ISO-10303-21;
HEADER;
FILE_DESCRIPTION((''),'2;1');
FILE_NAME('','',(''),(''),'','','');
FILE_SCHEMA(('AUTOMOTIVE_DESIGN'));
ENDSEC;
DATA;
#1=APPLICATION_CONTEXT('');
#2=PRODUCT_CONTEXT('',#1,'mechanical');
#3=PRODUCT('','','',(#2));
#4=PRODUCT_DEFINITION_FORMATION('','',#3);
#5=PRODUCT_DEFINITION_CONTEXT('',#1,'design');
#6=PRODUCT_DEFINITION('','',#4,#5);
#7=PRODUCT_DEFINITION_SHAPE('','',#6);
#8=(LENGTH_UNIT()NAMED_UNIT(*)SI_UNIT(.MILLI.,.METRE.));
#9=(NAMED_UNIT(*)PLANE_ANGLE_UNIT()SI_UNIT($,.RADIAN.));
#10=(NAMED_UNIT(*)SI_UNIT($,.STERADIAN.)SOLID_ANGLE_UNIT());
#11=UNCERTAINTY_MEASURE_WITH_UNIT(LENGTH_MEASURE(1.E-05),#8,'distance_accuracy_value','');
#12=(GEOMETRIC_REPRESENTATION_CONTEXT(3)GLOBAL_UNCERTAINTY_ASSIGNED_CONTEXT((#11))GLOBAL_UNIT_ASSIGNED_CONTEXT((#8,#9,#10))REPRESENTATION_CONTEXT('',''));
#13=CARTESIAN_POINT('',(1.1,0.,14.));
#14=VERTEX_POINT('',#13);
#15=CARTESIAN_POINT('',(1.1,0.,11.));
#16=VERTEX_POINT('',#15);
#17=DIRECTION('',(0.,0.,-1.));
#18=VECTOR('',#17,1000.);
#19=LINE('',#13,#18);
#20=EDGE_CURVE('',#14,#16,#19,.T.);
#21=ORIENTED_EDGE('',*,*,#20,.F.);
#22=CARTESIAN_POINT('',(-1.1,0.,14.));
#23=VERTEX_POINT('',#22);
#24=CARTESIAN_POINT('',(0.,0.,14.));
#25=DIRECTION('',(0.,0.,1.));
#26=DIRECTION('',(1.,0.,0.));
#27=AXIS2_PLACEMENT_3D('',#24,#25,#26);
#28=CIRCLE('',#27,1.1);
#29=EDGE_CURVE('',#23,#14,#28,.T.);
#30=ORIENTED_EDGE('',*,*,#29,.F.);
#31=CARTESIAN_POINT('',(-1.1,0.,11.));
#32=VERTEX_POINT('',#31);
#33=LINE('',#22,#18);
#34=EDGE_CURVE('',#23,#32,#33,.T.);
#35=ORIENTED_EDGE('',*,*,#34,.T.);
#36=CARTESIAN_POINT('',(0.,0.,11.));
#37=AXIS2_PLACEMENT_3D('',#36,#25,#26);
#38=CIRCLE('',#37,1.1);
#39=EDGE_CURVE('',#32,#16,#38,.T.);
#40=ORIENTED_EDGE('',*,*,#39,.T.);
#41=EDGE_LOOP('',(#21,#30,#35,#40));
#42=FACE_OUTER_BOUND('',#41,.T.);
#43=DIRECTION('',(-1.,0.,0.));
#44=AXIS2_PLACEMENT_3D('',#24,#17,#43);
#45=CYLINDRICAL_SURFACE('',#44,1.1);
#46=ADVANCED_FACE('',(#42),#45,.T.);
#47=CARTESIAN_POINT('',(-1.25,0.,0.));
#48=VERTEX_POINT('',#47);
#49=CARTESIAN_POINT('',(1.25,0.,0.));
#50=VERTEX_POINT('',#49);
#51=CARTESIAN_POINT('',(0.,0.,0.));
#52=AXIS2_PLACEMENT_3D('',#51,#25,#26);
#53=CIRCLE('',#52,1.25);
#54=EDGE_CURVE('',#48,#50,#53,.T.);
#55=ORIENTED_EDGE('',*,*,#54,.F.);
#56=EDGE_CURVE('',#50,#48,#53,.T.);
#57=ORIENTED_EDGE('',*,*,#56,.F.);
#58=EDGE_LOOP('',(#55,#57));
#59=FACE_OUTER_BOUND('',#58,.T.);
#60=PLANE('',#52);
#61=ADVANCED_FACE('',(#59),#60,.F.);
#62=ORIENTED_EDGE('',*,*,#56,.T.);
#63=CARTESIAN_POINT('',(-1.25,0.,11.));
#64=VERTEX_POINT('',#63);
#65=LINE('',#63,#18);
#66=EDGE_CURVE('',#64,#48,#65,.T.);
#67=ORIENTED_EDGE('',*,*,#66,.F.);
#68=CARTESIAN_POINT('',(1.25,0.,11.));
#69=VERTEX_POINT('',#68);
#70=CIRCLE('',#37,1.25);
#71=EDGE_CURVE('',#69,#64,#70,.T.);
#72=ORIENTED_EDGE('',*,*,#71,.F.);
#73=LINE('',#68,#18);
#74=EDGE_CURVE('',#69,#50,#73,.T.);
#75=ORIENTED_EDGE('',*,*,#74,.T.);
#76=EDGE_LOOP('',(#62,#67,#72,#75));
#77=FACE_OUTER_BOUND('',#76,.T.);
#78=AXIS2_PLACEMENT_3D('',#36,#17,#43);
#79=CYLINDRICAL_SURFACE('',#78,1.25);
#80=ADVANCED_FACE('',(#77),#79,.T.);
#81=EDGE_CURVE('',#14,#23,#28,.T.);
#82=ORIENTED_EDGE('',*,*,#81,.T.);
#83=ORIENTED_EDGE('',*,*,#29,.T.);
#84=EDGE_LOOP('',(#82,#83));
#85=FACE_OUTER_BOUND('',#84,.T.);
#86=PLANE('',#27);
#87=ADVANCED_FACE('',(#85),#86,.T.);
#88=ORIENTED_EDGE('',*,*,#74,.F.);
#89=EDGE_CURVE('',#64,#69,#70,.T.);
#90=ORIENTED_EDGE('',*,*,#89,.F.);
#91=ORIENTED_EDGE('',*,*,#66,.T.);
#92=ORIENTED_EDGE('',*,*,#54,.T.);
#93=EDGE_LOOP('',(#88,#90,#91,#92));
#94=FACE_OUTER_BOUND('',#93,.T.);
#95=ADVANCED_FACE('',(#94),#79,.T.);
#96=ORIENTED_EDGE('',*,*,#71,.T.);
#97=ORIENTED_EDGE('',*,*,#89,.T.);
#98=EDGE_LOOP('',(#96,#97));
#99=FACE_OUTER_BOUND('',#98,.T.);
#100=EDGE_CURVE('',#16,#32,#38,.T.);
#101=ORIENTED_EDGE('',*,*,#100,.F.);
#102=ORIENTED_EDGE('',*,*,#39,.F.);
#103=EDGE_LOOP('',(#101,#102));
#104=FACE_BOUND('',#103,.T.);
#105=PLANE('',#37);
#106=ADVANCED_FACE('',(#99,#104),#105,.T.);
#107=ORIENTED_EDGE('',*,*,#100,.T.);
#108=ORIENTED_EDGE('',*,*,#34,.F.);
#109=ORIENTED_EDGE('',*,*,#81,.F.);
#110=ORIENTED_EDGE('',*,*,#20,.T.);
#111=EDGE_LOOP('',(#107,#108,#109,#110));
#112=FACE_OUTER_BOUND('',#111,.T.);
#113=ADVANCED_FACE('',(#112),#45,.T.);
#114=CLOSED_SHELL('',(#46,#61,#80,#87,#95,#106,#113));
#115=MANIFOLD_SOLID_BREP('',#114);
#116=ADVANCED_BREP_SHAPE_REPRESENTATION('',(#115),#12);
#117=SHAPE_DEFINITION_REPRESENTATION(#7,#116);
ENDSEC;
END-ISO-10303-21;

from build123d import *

# Parameters (mm, degrees)
SKETCH_1_R      = 1.25
EXTRUDE_1_DEPTH = 11
SKETCH_2_R      = 1.1
EXTRUDE_2_DEPTH = 3


with BuildPart() as part:
    # 草图1 → 凸台-拉伸1 (new body)
    with BuildSketch(Plane.XY):
        Circle(SKETCH_1_R)
    extrude(amount=EXTRUDE_1_DEPTH)

    # 草图2 → 凸台-拉伸2 (add)
    with BuildSketch(Plane.XY.offset(11)):
        Circle(SKETCH_2_R)
    extrude(amount=EXTRUDE_2_DEPTH)


solid = part.part
